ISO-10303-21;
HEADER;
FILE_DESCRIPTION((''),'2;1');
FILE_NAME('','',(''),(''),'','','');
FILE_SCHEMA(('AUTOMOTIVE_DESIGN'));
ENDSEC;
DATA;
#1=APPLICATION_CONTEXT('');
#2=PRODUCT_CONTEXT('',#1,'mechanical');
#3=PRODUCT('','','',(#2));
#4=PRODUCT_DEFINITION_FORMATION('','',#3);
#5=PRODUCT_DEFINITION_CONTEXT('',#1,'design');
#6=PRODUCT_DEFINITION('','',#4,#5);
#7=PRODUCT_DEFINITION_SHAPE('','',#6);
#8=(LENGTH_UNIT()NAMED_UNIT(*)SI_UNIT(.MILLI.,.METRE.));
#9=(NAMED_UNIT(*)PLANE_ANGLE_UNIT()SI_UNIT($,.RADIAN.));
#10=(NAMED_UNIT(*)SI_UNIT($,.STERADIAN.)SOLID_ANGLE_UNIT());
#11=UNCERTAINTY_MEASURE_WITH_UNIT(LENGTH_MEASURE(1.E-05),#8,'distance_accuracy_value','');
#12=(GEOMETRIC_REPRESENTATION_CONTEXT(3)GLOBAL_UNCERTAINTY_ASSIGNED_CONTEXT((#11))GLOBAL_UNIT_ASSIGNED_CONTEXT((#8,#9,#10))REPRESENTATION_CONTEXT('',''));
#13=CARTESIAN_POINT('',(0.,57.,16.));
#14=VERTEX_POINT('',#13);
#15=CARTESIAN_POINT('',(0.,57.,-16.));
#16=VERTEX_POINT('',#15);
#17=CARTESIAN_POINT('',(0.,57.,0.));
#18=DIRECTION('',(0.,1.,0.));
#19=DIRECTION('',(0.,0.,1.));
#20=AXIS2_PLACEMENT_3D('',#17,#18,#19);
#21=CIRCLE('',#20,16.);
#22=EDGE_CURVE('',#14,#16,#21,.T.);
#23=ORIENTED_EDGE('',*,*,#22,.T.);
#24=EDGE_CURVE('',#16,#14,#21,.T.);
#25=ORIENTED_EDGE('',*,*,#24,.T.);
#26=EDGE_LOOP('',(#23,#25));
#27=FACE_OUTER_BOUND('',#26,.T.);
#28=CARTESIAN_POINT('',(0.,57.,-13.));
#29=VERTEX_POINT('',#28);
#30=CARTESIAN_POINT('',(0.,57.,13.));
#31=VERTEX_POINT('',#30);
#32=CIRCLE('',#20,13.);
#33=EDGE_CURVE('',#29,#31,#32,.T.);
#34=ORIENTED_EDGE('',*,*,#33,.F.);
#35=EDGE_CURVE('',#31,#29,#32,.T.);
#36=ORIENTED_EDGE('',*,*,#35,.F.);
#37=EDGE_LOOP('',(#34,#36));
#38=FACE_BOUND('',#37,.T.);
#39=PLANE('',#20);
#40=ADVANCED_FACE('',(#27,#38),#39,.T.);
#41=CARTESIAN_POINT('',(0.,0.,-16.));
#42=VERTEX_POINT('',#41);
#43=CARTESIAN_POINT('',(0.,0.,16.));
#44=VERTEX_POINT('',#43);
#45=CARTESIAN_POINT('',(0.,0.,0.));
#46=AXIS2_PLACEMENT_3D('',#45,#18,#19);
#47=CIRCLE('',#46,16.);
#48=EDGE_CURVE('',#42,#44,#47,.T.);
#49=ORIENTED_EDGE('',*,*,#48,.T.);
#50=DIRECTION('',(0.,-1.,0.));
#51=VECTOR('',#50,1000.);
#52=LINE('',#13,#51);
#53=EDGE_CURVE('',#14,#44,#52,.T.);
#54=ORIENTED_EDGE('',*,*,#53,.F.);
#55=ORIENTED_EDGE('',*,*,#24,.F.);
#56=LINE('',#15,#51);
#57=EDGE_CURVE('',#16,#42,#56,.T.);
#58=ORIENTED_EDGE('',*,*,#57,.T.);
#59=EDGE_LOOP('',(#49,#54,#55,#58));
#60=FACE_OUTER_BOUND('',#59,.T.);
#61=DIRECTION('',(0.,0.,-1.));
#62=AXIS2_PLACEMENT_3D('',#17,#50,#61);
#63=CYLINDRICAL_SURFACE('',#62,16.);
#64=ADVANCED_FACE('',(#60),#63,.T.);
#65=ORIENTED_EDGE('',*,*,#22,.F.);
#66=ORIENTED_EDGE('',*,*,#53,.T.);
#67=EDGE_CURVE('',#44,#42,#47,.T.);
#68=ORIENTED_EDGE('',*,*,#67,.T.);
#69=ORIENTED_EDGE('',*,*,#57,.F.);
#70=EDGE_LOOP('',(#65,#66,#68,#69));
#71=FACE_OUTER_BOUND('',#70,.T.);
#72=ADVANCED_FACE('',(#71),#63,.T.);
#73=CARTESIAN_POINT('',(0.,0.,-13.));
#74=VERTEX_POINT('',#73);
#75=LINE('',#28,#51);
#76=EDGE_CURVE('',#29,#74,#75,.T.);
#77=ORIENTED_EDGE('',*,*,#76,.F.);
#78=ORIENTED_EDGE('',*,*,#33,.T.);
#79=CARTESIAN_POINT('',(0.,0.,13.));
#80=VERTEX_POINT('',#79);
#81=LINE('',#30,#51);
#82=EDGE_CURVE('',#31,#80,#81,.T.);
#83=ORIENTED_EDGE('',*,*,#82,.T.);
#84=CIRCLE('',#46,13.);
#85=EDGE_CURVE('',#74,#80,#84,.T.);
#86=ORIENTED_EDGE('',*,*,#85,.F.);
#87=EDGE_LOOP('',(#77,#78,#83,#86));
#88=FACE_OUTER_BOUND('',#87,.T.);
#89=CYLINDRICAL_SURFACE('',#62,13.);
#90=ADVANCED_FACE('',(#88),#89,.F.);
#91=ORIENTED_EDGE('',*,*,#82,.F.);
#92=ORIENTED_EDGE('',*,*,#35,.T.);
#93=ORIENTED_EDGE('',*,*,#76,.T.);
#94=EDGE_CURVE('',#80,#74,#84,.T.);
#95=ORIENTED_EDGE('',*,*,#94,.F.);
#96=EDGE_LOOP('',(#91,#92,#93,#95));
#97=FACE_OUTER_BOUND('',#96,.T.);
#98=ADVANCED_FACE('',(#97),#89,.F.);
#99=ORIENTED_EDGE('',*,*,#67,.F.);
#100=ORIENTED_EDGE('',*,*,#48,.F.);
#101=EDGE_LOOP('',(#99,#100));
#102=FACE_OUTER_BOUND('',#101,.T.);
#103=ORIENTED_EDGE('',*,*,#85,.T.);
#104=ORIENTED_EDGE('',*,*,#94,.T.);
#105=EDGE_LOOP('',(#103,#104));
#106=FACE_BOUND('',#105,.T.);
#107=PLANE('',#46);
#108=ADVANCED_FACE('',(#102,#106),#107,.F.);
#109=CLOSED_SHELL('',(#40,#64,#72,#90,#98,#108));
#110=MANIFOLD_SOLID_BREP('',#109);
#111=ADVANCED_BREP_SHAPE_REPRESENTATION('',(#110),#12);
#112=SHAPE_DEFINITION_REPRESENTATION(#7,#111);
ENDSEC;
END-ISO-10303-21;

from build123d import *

# Parameters (mm, degrees)
SKETCH1_R           = 16
SKETCH1_R_2         = 13
BOSS_EXTRUDE1_DEPTH = 57


with BuildPart() as part:
    # Sketch1 → Boss-Extrude1 (new body)
    with BuildSketch(Plane(origin=(0, 0, 0), x_dir=(1, 0, 0), z_dir=(0, 1, 0))):
        with Locations(Location((0, 0, 0), (0, 0, 90))):
            Circle(SKETCH1_R)
        with Locations(Location((0, 0, 0), (0, 0, 90))):
            Circle(SKETCH1_R_2, mode=Mode.SUBTRACT)
    extrude(amount=BOSS_EXTRUDE1_DEPTH)


solid = part.part
